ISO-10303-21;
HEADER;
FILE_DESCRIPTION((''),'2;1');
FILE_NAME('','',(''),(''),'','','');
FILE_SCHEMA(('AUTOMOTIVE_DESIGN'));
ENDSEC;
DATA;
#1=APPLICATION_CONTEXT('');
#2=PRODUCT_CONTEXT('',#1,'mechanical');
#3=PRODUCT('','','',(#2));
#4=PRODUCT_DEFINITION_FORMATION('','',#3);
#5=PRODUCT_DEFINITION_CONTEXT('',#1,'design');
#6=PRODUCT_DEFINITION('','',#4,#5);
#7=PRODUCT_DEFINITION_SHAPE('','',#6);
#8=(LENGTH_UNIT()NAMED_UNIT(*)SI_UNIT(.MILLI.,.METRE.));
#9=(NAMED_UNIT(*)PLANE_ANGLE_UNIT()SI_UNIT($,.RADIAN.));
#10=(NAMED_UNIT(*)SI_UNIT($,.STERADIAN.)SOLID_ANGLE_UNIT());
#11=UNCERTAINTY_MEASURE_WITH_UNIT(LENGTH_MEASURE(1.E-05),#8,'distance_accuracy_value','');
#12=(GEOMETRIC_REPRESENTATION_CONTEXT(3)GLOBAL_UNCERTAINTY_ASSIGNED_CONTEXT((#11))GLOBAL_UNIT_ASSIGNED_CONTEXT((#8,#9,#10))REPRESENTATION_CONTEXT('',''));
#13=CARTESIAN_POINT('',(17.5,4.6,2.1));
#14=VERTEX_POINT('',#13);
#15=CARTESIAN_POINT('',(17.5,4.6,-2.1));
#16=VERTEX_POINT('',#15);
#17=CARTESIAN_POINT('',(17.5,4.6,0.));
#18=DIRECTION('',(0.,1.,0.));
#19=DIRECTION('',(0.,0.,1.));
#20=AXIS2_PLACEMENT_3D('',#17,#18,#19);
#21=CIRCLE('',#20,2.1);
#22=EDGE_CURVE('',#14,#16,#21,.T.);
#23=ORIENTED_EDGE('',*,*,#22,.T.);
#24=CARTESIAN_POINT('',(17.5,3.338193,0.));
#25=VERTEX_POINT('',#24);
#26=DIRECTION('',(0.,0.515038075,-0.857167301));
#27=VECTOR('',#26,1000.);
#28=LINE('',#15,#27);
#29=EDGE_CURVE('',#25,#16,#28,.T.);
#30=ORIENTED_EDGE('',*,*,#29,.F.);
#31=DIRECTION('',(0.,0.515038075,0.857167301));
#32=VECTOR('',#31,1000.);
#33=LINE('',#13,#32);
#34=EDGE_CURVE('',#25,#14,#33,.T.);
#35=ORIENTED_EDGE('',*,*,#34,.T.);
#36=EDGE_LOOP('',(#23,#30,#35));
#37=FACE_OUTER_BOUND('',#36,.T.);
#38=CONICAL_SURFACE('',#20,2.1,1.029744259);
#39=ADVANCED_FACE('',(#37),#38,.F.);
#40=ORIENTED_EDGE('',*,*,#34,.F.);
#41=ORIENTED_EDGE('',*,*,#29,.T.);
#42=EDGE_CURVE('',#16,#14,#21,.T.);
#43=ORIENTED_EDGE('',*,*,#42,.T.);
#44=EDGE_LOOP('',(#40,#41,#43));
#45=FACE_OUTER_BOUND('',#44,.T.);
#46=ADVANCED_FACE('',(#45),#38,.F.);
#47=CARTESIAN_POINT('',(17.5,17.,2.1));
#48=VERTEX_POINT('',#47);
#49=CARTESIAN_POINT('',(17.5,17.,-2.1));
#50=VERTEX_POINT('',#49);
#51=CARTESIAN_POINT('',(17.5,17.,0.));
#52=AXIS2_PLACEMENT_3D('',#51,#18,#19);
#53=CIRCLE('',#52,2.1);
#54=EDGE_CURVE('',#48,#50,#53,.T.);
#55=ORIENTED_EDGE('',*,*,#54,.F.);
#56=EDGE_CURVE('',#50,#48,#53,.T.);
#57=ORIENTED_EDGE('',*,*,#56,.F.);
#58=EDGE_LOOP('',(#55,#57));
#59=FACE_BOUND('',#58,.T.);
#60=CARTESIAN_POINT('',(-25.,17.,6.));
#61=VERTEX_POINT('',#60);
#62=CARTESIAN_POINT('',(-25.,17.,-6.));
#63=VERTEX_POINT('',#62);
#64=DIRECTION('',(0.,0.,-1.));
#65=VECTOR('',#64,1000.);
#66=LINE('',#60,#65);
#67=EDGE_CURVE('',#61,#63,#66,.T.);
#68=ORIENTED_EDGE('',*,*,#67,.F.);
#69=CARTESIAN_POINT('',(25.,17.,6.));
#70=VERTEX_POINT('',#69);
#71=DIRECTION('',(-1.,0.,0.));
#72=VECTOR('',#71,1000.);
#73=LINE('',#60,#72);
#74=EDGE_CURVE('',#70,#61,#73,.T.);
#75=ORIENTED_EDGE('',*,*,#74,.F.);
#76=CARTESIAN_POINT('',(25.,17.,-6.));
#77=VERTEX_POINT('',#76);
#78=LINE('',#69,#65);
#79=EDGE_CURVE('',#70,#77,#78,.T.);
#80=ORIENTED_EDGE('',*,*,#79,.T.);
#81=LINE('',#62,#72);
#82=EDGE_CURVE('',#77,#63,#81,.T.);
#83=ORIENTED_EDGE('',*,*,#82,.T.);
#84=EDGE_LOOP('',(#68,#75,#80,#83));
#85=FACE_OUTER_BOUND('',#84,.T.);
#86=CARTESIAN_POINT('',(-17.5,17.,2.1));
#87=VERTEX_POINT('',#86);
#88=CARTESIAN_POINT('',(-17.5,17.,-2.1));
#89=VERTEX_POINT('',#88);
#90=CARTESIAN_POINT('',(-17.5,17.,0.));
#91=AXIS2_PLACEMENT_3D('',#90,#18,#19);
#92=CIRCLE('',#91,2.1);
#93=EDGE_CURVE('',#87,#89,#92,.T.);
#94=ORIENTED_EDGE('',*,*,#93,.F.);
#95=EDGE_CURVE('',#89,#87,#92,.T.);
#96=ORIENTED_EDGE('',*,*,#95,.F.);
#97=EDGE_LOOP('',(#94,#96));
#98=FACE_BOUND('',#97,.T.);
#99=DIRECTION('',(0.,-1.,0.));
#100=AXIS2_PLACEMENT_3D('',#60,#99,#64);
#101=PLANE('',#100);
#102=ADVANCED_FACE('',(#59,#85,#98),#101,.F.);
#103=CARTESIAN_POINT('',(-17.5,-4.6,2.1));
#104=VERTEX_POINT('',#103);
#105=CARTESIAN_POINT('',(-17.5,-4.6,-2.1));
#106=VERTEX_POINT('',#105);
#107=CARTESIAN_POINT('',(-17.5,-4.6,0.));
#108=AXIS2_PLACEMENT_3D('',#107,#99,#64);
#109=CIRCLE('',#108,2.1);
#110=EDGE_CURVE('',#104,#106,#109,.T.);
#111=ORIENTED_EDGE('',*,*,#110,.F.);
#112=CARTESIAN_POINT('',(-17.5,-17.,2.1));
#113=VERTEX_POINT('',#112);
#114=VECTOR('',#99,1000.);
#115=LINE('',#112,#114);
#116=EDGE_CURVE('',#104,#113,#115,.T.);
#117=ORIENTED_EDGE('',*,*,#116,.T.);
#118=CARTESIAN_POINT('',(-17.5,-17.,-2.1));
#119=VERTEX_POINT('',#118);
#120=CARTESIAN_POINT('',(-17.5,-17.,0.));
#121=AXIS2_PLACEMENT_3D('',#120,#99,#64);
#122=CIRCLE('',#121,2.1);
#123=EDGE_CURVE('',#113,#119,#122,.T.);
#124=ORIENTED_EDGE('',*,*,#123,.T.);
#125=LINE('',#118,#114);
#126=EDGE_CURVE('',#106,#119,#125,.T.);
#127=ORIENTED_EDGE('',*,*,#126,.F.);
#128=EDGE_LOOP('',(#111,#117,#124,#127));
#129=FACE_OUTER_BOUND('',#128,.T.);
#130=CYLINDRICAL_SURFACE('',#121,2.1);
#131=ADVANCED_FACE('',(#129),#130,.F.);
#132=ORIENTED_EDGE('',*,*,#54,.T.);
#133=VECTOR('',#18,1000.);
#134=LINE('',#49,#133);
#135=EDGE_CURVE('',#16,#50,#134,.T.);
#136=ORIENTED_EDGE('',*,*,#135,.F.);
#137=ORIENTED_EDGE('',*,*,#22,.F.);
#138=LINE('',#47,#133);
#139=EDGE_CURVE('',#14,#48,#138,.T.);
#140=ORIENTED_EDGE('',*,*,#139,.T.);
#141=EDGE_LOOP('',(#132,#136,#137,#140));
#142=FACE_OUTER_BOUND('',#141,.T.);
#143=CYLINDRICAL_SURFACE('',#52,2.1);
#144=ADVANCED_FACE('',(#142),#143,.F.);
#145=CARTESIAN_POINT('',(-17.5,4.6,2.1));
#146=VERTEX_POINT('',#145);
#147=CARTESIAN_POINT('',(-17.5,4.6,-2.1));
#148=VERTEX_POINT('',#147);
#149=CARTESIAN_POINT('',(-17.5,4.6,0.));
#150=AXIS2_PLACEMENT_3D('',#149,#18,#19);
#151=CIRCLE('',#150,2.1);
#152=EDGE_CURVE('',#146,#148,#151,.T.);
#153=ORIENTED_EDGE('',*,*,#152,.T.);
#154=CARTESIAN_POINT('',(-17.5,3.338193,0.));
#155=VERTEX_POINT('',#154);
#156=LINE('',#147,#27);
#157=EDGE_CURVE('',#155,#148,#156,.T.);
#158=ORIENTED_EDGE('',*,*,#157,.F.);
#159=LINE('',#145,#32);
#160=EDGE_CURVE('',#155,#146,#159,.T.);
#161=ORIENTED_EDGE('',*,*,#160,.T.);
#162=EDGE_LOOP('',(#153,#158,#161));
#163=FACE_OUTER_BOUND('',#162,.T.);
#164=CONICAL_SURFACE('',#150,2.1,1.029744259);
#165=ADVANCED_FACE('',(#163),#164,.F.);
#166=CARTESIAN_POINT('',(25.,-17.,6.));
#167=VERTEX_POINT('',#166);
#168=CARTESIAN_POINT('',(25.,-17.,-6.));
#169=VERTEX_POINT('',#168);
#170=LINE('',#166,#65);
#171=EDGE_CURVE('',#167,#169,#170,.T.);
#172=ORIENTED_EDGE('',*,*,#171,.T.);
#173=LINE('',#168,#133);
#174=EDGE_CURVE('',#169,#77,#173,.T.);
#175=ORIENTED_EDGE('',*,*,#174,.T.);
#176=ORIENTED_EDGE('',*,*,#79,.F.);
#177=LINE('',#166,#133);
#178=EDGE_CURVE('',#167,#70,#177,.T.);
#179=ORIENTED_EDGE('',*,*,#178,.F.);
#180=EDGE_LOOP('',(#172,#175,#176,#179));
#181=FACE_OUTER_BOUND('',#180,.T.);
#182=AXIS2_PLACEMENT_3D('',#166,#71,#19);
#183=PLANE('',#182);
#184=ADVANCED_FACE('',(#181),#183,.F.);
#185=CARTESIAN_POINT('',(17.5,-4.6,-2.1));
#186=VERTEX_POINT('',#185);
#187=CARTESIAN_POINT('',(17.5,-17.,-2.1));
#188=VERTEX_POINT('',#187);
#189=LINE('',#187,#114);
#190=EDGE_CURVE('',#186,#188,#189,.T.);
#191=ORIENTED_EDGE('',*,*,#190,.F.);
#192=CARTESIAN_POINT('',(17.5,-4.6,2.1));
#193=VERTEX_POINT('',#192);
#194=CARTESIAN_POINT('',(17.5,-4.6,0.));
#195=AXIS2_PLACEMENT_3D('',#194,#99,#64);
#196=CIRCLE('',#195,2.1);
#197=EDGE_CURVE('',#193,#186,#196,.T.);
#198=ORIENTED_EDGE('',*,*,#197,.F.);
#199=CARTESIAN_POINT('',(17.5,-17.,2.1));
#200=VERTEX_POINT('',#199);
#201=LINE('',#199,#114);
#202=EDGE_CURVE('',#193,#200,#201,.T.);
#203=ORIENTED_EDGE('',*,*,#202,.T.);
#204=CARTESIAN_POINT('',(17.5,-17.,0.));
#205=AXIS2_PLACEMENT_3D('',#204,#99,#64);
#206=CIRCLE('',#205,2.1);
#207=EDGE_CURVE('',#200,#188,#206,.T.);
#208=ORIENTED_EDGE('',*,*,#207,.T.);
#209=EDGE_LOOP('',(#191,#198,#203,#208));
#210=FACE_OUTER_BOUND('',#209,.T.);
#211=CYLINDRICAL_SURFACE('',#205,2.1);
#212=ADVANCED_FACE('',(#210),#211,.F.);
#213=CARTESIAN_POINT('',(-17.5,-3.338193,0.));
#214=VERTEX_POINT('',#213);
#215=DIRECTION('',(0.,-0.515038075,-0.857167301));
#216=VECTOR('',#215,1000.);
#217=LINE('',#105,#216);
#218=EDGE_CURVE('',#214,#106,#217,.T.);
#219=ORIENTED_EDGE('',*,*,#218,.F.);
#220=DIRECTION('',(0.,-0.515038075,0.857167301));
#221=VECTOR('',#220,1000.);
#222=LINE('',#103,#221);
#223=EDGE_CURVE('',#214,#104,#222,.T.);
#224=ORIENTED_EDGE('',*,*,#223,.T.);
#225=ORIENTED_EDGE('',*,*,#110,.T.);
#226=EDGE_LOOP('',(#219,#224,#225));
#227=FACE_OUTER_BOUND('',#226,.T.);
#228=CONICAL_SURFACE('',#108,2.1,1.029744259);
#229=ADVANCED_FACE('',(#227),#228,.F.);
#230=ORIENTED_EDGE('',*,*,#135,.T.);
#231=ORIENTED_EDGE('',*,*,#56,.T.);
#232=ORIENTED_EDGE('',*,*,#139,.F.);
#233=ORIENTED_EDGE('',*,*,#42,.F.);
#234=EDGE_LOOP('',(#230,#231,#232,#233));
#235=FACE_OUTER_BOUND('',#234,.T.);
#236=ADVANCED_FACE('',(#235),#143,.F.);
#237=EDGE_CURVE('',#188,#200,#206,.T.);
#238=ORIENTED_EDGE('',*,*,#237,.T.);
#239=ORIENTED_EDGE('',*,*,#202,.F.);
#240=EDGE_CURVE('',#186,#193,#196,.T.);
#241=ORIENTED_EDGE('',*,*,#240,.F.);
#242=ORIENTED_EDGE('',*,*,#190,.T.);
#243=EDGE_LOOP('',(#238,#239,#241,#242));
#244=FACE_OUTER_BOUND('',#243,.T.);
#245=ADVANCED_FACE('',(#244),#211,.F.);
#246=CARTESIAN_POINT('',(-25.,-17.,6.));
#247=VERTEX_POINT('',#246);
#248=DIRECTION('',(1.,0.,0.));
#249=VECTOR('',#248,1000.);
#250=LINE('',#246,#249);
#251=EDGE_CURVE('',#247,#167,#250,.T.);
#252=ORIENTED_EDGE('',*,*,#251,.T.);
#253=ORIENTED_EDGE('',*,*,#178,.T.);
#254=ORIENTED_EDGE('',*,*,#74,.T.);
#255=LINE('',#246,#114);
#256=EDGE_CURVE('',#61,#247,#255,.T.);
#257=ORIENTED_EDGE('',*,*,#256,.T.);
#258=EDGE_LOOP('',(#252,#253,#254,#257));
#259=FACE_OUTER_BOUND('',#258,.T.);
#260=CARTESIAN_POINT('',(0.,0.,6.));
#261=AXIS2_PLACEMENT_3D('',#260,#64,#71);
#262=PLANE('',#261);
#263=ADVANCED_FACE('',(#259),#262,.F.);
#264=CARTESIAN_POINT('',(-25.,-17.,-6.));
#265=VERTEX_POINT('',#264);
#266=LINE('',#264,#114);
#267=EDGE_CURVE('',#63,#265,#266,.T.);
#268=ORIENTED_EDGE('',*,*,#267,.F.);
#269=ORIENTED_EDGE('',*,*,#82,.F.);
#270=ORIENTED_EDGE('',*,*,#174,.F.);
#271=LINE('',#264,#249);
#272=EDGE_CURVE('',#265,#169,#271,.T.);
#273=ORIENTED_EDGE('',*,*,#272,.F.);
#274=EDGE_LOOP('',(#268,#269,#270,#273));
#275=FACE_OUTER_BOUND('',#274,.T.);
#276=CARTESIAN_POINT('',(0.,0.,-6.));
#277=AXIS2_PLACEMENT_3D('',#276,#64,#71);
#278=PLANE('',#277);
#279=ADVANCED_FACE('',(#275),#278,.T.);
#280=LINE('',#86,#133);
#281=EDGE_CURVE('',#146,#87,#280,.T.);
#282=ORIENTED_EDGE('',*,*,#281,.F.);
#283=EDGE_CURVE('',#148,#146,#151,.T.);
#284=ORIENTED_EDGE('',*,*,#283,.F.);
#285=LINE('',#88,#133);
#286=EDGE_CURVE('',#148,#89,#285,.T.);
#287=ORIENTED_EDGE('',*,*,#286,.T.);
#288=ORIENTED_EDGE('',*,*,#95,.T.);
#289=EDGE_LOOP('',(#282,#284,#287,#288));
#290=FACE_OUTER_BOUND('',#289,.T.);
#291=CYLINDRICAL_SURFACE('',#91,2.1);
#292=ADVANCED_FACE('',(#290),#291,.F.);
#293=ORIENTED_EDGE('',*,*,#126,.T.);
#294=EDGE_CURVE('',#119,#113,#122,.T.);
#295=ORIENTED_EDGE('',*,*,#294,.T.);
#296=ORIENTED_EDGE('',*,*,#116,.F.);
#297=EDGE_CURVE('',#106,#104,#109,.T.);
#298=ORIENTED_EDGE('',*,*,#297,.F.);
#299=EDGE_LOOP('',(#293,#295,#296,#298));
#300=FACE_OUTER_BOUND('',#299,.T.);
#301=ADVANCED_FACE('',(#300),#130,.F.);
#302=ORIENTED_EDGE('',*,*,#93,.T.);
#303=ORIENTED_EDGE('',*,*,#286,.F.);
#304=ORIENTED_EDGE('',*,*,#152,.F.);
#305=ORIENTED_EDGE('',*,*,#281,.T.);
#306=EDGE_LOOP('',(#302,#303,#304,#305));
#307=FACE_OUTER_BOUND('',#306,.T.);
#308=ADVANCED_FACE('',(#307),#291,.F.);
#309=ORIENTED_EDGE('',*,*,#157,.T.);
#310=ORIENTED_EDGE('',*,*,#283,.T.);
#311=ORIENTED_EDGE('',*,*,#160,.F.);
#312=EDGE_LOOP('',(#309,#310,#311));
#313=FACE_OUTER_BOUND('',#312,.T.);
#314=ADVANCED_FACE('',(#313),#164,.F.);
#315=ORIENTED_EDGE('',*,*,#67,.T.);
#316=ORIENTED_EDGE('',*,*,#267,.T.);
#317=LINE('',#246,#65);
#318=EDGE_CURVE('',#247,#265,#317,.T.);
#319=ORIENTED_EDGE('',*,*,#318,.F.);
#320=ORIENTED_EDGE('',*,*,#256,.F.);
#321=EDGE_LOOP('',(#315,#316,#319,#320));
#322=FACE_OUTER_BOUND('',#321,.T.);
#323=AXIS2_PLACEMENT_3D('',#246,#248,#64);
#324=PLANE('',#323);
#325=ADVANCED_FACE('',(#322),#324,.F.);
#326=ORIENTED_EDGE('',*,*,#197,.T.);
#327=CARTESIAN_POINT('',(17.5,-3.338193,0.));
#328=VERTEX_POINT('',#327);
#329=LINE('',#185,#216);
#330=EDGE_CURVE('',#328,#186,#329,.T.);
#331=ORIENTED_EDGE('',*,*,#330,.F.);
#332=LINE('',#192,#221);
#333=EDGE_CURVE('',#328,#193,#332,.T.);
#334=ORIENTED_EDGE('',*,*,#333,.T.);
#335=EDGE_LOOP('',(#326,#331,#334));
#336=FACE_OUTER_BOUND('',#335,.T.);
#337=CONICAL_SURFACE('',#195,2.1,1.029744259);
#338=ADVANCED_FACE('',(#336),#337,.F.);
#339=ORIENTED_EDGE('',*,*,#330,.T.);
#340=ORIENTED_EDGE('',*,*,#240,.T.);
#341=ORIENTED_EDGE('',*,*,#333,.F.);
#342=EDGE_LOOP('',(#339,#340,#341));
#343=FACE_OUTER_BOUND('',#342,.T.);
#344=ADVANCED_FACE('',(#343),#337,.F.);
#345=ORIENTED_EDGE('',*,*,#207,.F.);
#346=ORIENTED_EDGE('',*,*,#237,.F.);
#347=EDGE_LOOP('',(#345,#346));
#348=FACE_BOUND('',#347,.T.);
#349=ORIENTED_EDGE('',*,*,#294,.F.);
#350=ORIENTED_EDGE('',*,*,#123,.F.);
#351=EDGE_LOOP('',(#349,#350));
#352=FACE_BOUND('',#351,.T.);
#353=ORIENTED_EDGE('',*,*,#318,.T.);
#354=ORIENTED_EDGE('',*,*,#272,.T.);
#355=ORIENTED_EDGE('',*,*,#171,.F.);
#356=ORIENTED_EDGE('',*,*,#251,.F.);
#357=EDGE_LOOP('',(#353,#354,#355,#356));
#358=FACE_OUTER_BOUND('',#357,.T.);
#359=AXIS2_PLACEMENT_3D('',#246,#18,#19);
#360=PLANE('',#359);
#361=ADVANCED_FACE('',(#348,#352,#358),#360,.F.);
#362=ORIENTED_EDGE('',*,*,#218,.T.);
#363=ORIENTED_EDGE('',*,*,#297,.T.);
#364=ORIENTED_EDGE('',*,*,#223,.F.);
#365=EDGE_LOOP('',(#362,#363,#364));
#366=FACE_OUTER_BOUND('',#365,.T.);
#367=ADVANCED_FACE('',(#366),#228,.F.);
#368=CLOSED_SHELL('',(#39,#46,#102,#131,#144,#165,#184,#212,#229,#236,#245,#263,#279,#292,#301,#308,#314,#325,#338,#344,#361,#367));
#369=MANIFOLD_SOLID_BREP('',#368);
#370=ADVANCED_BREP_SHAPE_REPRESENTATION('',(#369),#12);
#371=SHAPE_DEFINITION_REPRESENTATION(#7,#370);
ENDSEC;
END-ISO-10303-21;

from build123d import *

# Parameters (mm, degrees)
SKETCH_1_W                  = 50
SKETCH_1_H                  = 34
EXTRUDE_1_DEPTH             = 6
HOLE_WIZARD_M5_1_AT_2_COUNT = 2
HOLE_WIZARD_M5_1_AT_2_PITCH = 35


with BuildPart() as part:
    # 草图1 → 凸台-拉伸1 (new, symmetric)
    with BuildSketch(Plane.XY):
        Rectangle(SKETCH_1_W, SKETCH_1_H)
    extrude(amount=EXTRUDE_1_DEPTH, both=True)

    # 草图3 → M5 螺纹孔1 (revolve, cut)
    with BuildSketch(Plane(origin=(-17.5, -17, 0), x_dir=(0, 0, -1), z_dir=(1, 0, 0))):
        Polygon((0, 0), (0, 13.6618073), (2.1, 12.4), (2.1, 0), align=None)
    hole_wizard_m5_1 = revolve(axis=Axis((-17.5, -23.35, 0), (0, 1, 0)), mode=Mode.SUBTRACT)

    # M5 螺纹孔1 at 2: M5 螺纹孔1 ×2
    with Locations(*[(i * HOLE_WIZARD_M5_1_AT_2_PITCH, 0, 0) for i in range(1, HOLE_WIZARD_M5_1_AT_2_COUNT)]):
        add(hole_wizard_m5_1, mode=Mode.SUBTRACT)

    # 镜向1: M5 螺纹孔1 across plane
    add(hole_wizard_m5_1.mirror(Plane.ZX), mode=Mode.SUBTRACT)

    # 镜向1 copy 1 sketch → 镜向1 copy 1 (revolve, cut)
    with BuildSketch(Plane(origin=(17.5, 17, 0), x_dir=(0, 0, -1), z_dir=(1, 0, 0))):
        Polygon((0, 0), (0, -13.6618073), (2.1, -12.4), (2.1, 0), align=None)
    revolve(axis=Axis((17.5, 23.35, 0), (0, 1, 0)), mode=Mode.SUBTRACT)


solid = part.part
